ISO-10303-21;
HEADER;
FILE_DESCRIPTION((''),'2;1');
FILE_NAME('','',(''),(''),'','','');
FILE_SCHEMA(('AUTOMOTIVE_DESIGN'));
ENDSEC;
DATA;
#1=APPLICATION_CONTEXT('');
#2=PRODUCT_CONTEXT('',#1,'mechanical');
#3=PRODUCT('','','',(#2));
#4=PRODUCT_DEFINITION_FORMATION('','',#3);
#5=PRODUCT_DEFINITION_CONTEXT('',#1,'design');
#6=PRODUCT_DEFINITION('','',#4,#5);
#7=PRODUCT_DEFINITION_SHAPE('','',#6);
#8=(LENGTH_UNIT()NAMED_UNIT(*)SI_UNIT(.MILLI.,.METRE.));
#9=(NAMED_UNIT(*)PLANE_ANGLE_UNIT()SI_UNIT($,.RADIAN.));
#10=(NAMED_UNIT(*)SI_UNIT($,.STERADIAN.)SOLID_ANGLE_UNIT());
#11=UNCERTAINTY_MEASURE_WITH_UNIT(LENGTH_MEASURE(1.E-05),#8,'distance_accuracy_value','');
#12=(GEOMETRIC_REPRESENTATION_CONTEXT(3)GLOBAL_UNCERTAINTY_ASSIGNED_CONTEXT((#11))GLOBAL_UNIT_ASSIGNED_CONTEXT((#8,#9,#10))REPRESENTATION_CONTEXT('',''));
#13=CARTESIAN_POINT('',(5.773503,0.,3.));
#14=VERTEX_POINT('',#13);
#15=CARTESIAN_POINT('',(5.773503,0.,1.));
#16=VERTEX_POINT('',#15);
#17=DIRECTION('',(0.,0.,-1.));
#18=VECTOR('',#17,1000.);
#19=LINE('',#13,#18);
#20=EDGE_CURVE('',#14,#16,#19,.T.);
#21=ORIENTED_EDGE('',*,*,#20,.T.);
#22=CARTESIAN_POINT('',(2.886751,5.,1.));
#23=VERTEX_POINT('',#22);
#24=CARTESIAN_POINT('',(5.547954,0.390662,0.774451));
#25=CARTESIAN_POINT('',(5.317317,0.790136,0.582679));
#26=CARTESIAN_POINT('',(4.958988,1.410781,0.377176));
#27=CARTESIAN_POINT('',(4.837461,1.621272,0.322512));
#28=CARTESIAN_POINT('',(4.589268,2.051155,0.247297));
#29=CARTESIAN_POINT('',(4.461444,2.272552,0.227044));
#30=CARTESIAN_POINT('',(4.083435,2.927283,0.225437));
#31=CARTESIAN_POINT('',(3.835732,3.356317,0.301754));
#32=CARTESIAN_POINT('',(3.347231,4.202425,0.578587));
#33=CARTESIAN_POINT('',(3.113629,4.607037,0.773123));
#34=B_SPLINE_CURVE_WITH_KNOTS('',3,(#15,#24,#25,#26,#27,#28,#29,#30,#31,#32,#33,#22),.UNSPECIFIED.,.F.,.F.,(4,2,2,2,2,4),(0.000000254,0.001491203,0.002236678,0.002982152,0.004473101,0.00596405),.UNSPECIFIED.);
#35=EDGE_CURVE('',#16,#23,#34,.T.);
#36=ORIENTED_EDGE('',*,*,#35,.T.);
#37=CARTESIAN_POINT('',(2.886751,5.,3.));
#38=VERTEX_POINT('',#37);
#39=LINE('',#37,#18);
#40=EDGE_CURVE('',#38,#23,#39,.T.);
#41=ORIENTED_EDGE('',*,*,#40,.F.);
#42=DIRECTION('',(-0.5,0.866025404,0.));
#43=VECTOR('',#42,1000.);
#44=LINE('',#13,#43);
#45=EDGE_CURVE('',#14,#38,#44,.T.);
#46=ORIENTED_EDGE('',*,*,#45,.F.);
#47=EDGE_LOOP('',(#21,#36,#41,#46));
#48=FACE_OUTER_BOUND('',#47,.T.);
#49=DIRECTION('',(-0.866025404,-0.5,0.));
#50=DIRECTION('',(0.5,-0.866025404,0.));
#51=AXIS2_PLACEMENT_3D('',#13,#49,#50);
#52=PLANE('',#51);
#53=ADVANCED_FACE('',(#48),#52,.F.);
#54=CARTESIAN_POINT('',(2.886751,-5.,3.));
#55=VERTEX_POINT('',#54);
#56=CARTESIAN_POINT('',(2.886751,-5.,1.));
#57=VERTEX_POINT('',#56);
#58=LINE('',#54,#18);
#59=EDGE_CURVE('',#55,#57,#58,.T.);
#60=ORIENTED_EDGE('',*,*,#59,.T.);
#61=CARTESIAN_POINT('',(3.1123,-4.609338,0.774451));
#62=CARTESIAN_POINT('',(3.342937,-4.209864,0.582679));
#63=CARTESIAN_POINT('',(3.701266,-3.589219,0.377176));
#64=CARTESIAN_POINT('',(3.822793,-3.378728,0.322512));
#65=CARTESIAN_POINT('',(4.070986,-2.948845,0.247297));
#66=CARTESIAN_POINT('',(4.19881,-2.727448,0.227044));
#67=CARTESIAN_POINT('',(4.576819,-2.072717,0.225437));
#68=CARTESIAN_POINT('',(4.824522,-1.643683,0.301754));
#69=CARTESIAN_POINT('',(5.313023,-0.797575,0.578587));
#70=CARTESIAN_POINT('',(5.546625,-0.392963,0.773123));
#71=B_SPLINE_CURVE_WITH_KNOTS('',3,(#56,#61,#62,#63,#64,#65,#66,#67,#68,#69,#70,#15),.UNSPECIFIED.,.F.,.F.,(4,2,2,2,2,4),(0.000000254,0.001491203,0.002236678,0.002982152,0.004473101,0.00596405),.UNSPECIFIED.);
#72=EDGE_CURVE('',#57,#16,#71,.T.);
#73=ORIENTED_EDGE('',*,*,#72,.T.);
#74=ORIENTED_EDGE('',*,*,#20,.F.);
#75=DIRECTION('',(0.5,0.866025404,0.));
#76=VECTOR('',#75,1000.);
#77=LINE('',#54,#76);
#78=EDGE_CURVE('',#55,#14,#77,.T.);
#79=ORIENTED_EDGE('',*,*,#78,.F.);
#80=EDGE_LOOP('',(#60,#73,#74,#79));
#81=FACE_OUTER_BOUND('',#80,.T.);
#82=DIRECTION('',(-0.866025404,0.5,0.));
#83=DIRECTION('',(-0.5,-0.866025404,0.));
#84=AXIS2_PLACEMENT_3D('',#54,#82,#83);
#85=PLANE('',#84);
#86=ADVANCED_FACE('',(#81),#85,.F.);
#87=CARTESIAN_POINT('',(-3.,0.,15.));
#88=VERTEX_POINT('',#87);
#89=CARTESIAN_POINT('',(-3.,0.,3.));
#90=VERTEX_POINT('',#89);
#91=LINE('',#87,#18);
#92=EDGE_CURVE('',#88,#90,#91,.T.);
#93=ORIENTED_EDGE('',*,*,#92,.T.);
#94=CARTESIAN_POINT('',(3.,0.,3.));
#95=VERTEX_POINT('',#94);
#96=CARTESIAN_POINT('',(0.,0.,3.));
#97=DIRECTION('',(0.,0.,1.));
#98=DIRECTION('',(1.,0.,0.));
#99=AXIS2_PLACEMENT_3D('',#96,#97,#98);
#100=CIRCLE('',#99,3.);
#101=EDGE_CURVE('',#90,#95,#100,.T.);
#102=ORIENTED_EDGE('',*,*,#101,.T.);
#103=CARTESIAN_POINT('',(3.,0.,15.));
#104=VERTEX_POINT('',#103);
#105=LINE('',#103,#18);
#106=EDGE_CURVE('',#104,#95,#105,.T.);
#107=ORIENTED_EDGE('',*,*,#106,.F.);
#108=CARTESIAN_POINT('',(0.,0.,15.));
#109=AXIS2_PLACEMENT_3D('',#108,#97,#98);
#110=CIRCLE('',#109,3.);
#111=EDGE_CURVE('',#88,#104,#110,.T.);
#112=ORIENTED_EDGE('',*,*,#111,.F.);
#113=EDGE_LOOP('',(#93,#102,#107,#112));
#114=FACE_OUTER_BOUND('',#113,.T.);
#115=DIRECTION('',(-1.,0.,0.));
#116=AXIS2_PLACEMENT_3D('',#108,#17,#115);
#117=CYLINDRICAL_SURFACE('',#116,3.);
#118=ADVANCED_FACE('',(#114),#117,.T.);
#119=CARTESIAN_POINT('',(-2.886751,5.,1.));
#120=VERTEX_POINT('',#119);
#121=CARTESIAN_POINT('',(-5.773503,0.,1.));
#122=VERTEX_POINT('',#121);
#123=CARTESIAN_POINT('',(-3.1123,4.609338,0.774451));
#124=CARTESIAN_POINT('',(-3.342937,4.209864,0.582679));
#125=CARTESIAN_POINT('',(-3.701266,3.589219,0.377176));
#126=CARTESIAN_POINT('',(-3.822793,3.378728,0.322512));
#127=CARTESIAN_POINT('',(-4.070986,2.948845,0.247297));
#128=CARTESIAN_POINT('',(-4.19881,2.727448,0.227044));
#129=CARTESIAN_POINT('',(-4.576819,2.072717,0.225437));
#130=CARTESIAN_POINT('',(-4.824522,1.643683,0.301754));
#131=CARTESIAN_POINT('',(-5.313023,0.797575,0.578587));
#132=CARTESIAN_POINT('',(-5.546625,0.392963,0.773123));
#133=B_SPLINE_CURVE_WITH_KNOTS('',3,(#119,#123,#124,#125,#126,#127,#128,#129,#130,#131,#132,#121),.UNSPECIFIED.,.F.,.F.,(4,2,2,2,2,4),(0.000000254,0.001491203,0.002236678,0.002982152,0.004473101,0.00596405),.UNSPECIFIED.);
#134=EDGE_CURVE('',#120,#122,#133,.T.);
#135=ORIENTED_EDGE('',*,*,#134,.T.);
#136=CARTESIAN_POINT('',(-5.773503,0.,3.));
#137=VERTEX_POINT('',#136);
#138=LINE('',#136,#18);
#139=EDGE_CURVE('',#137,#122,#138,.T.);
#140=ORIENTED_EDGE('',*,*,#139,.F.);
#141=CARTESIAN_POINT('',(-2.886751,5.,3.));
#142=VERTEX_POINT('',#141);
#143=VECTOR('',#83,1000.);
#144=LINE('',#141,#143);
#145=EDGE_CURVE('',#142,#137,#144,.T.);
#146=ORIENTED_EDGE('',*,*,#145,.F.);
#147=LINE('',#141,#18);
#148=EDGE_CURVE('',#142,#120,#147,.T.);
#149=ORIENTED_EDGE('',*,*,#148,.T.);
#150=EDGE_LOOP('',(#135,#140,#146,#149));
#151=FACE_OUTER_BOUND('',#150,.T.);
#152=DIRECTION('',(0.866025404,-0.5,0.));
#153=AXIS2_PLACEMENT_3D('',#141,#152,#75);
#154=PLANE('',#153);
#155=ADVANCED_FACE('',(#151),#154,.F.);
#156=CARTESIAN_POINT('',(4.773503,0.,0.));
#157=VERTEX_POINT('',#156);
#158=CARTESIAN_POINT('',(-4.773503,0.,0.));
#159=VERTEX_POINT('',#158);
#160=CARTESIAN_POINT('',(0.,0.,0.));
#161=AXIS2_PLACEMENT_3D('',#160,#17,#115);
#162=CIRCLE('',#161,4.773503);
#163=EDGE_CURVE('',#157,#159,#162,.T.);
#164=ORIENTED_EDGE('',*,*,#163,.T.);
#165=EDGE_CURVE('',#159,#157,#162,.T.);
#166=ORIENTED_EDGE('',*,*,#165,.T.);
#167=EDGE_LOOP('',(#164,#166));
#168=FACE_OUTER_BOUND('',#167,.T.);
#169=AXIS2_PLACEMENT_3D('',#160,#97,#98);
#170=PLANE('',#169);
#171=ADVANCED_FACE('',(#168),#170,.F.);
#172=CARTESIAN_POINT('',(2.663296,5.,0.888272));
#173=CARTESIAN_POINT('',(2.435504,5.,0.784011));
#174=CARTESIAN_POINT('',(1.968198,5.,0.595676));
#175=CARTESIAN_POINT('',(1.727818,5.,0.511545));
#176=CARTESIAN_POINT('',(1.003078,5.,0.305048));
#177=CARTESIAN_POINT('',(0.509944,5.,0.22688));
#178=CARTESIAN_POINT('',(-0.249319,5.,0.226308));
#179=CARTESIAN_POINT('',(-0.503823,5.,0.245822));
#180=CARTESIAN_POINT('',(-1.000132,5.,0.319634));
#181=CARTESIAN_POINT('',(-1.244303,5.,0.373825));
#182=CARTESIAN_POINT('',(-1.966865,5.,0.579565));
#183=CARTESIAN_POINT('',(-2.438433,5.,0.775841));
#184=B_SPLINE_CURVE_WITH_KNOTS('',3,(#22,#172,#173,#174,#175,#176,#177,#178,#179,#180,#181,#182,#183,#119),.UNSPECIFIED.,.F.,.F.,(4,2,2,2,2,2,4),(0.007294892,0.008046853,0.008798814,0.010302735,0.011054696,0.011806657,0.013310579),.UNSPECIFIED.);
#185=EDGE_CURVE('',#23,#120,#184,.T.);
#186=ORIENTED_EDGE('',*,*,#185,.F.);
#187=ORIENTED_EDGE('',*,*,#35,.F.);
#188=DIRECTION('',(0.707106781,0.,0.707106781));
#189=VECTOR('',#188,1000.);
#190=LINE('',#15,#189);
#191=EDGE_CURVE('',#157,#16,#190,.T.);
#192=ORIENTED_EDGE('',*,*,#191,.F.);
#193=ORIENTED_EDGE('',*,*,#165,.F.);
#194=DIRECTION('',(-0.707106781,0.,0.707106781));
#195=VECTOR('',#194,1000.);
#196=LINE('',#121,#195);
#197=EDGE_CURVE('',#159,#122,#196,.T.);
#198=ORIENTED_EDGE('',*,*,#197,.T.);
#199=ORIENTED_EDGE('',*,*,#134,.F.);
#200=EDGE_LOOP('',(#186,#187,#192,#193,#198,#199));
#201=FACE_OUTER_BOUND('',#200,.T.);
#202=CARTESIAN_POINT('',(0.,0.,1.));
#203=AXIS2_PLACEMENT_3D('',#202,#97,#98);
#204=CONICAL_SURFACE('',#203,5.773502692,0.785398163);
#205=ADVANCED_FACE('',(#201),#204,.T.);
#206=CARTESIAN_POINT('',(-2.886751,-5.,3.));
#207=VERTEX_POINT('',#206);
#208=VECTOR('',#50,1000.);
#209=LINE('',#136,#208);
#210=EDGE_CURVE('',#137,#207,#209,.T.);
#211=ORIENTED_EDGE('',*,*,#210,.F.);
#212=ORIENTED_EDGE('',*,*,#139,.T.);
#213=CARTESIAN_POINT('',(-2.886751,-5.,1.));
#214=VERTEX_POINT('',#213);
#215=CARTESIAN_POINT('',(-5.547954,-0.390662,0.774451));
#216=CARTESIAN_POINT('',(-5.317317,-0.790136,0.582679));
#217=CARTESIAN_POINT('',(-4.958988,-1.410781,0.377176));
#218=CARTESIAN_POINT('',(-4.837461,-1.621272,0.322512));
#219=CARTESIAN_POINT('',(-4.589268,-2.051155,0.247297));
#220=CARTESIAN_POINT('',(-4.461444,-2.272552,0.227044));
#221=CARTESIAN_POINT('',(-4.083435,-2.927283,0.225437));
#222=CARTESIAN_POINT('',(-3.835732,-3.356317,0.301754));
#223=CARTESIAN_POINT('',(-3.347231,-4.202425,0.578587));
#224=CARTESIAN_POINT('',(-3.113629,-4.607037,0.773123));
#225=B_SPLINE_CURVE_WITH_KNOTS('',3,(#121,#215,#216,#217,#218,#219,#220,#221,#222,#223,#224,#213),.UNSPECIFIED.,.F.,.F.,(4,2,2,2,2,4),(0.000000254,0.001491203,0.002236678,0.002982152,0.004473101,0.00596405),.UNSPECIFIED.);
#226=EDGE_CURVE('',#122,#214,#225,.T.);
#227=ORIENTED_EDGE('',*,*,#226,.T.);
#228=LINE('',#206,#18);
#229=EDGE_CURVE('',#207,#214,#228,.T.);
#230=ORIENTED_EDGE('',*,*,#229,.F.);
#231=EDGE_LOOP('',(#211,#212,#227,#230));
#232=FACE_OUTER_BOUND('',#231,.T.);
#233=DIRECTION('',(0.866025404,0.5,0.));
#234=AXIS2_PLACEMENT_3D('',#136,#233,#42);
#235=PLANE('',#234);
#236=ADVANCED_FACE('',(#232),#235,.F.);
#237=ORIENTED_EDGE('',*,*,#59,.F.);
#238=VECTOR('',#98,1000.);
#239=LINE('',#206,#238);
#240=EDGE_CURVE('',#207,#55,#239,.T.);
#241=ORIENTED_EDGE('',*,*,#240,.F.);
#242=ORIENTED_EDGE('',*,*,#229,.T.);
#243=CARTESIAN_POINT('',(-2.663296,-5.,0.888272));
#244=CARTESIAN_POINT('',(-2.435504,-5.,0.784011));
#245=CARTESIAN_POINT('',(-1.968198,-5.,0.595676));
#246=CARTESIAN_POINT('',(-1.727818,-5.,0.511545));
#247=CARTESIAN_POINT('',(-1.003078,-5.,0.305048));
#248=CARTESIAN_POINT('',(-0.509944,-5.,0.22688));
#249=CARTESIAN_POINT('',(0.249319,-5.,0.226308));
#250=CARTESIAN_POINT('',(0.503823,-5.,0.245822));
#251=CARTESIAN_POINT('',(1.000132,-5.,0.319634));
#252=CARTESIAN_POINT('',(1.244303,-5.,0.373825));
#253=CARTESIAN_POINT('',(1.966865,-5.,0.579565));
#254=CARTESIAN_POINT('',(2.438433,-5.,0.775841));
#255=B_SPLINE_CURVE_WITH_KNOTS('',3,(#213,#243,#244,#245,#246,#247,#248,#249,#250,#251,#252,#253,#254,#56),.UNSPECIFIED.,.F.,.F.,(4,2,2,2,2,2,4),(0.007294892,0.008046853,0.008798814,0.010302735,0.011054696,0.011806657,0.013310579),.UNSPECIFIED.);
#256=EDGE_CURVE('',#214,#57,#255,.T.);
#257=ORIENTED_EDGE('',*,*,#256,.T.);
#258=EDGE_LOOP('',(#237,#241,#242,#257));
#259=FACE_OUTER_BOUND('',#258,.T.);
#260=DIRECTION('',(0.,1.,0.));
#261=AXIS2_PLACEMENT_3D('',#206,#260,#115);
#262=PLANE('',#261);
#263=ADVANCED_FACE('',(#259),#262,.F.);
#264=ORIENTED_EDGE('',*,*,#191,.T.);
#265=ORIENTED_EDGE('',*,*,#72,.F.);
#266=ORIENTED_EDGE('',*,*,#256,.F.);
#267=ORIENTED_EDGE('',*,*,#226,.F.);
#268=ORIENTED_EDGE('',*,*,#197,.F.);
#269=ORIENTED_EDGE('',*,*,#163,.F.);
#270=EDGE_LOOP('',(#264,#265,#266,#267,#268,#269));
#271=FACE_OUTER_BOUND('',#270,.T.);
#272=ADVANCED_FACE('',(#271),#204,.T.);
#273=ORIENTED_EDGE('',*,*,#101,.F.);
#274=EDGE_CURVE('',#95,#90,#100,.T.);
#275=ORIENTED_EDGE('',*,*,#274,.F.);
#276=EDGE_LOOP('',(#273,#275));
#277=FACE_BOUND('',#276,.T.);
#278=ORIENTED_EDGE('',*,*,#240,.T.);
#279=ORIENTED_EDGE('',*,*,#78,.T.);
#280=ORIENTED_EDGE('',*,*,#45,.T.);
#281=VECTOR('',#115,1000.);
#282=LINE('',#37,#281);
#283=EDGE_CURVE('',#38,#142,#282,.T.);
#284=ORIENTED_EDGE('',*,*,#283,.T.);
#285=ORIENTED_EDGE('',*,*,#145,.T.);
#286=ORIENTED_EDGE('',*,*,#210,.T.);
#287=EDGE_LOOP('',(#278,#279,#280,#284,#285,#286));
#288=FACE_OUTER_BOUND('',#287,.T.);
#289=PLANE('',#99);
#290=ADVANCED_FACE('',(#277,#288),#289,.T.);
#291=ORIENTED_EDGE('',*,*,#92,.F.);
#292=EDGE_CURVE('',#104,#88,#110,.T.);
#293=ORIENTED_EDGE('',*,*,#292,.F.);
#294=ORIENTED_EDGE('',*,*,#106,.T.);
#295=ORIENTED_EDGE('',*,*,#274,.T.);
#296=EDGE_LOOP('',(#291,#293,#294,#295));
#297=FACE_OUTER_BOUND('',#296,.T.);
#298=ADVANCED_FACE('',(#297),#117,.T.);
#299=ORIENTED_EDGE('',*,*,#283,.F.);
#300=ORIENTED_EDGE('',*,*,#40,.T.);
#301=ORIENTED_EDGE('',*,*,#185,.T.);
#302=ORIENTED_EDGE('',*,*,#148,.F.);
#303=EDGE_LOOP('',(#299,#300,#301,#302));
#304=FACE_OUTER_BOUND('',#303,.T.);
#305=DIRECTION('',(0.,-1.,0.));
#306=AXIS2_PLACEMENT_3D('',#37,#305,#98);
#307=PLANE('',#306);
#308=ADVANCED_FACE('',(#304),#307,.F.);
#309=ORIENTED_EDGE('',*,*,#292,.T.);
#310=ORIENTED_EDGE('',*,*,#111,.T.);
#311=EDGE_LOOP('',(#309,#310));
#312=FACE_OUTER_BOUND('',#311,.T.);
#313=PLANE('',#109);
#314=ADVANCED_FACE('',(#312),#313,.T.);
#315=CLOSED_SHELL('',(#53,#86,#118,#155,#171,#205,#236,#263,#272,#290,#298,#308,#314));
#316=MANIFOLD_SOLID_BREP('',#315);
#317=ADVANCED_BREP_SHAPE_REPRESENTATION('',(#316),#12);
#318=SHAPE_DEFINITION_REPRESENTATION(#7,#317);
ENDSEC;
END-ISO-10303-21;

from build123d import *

# Parameters (mm, degrees)
HEX_HEAD_DEPTH    = 3
SHANK_PROFILE_6_R = 3
SHANK_6X12_DEPTH  = 12


with BuildPart() as part:
    # Hex Head Profile 10AF → Hex Head (new body)
    with BuildSketch(Plane.XY):
        Polygon((-2.886751346, 5), (-5.773502692, 0), (-2.886751346, -5), (2.886751346, -5), (5.773502692, 0), (2.886751346, 5), align=None)
    extrude(amount=HEX_HEAD_DEPTH)

    # Shank Profile Ø6 → Shank Ø6x12 (add)
    with BuildSketch(Plane.XY.offset(3)):
        Circle(SHANK_PROFILE_6_R)
    extrude(amount=SHANK_6X12_DEPTH)

    # Head Chamfer Profile → Head Chamfer 45x1 (revolve, cut)
    with BuildSketch(Plane(origin=(0, 0, 0), x_dir=(1, 0, 0), z_dir=(0, 1, 0)), mode=Mode.PRIVATE) as head_chamfer_45x1_sk:
        Polygon((-4.773502692, 0), (-5.773502692, 0), (-5.773502692, -1), align=None)
    revolve(head_chamfer_45x1_sk.sketch.rotate(Axis((0, 0, -2.775923962), (0, 0, 1)), 180), axis=Axis((0, 0, -2.775923962), (0, 0, 1)), mode=Mode.SUBTRACT)


solid = part.part
